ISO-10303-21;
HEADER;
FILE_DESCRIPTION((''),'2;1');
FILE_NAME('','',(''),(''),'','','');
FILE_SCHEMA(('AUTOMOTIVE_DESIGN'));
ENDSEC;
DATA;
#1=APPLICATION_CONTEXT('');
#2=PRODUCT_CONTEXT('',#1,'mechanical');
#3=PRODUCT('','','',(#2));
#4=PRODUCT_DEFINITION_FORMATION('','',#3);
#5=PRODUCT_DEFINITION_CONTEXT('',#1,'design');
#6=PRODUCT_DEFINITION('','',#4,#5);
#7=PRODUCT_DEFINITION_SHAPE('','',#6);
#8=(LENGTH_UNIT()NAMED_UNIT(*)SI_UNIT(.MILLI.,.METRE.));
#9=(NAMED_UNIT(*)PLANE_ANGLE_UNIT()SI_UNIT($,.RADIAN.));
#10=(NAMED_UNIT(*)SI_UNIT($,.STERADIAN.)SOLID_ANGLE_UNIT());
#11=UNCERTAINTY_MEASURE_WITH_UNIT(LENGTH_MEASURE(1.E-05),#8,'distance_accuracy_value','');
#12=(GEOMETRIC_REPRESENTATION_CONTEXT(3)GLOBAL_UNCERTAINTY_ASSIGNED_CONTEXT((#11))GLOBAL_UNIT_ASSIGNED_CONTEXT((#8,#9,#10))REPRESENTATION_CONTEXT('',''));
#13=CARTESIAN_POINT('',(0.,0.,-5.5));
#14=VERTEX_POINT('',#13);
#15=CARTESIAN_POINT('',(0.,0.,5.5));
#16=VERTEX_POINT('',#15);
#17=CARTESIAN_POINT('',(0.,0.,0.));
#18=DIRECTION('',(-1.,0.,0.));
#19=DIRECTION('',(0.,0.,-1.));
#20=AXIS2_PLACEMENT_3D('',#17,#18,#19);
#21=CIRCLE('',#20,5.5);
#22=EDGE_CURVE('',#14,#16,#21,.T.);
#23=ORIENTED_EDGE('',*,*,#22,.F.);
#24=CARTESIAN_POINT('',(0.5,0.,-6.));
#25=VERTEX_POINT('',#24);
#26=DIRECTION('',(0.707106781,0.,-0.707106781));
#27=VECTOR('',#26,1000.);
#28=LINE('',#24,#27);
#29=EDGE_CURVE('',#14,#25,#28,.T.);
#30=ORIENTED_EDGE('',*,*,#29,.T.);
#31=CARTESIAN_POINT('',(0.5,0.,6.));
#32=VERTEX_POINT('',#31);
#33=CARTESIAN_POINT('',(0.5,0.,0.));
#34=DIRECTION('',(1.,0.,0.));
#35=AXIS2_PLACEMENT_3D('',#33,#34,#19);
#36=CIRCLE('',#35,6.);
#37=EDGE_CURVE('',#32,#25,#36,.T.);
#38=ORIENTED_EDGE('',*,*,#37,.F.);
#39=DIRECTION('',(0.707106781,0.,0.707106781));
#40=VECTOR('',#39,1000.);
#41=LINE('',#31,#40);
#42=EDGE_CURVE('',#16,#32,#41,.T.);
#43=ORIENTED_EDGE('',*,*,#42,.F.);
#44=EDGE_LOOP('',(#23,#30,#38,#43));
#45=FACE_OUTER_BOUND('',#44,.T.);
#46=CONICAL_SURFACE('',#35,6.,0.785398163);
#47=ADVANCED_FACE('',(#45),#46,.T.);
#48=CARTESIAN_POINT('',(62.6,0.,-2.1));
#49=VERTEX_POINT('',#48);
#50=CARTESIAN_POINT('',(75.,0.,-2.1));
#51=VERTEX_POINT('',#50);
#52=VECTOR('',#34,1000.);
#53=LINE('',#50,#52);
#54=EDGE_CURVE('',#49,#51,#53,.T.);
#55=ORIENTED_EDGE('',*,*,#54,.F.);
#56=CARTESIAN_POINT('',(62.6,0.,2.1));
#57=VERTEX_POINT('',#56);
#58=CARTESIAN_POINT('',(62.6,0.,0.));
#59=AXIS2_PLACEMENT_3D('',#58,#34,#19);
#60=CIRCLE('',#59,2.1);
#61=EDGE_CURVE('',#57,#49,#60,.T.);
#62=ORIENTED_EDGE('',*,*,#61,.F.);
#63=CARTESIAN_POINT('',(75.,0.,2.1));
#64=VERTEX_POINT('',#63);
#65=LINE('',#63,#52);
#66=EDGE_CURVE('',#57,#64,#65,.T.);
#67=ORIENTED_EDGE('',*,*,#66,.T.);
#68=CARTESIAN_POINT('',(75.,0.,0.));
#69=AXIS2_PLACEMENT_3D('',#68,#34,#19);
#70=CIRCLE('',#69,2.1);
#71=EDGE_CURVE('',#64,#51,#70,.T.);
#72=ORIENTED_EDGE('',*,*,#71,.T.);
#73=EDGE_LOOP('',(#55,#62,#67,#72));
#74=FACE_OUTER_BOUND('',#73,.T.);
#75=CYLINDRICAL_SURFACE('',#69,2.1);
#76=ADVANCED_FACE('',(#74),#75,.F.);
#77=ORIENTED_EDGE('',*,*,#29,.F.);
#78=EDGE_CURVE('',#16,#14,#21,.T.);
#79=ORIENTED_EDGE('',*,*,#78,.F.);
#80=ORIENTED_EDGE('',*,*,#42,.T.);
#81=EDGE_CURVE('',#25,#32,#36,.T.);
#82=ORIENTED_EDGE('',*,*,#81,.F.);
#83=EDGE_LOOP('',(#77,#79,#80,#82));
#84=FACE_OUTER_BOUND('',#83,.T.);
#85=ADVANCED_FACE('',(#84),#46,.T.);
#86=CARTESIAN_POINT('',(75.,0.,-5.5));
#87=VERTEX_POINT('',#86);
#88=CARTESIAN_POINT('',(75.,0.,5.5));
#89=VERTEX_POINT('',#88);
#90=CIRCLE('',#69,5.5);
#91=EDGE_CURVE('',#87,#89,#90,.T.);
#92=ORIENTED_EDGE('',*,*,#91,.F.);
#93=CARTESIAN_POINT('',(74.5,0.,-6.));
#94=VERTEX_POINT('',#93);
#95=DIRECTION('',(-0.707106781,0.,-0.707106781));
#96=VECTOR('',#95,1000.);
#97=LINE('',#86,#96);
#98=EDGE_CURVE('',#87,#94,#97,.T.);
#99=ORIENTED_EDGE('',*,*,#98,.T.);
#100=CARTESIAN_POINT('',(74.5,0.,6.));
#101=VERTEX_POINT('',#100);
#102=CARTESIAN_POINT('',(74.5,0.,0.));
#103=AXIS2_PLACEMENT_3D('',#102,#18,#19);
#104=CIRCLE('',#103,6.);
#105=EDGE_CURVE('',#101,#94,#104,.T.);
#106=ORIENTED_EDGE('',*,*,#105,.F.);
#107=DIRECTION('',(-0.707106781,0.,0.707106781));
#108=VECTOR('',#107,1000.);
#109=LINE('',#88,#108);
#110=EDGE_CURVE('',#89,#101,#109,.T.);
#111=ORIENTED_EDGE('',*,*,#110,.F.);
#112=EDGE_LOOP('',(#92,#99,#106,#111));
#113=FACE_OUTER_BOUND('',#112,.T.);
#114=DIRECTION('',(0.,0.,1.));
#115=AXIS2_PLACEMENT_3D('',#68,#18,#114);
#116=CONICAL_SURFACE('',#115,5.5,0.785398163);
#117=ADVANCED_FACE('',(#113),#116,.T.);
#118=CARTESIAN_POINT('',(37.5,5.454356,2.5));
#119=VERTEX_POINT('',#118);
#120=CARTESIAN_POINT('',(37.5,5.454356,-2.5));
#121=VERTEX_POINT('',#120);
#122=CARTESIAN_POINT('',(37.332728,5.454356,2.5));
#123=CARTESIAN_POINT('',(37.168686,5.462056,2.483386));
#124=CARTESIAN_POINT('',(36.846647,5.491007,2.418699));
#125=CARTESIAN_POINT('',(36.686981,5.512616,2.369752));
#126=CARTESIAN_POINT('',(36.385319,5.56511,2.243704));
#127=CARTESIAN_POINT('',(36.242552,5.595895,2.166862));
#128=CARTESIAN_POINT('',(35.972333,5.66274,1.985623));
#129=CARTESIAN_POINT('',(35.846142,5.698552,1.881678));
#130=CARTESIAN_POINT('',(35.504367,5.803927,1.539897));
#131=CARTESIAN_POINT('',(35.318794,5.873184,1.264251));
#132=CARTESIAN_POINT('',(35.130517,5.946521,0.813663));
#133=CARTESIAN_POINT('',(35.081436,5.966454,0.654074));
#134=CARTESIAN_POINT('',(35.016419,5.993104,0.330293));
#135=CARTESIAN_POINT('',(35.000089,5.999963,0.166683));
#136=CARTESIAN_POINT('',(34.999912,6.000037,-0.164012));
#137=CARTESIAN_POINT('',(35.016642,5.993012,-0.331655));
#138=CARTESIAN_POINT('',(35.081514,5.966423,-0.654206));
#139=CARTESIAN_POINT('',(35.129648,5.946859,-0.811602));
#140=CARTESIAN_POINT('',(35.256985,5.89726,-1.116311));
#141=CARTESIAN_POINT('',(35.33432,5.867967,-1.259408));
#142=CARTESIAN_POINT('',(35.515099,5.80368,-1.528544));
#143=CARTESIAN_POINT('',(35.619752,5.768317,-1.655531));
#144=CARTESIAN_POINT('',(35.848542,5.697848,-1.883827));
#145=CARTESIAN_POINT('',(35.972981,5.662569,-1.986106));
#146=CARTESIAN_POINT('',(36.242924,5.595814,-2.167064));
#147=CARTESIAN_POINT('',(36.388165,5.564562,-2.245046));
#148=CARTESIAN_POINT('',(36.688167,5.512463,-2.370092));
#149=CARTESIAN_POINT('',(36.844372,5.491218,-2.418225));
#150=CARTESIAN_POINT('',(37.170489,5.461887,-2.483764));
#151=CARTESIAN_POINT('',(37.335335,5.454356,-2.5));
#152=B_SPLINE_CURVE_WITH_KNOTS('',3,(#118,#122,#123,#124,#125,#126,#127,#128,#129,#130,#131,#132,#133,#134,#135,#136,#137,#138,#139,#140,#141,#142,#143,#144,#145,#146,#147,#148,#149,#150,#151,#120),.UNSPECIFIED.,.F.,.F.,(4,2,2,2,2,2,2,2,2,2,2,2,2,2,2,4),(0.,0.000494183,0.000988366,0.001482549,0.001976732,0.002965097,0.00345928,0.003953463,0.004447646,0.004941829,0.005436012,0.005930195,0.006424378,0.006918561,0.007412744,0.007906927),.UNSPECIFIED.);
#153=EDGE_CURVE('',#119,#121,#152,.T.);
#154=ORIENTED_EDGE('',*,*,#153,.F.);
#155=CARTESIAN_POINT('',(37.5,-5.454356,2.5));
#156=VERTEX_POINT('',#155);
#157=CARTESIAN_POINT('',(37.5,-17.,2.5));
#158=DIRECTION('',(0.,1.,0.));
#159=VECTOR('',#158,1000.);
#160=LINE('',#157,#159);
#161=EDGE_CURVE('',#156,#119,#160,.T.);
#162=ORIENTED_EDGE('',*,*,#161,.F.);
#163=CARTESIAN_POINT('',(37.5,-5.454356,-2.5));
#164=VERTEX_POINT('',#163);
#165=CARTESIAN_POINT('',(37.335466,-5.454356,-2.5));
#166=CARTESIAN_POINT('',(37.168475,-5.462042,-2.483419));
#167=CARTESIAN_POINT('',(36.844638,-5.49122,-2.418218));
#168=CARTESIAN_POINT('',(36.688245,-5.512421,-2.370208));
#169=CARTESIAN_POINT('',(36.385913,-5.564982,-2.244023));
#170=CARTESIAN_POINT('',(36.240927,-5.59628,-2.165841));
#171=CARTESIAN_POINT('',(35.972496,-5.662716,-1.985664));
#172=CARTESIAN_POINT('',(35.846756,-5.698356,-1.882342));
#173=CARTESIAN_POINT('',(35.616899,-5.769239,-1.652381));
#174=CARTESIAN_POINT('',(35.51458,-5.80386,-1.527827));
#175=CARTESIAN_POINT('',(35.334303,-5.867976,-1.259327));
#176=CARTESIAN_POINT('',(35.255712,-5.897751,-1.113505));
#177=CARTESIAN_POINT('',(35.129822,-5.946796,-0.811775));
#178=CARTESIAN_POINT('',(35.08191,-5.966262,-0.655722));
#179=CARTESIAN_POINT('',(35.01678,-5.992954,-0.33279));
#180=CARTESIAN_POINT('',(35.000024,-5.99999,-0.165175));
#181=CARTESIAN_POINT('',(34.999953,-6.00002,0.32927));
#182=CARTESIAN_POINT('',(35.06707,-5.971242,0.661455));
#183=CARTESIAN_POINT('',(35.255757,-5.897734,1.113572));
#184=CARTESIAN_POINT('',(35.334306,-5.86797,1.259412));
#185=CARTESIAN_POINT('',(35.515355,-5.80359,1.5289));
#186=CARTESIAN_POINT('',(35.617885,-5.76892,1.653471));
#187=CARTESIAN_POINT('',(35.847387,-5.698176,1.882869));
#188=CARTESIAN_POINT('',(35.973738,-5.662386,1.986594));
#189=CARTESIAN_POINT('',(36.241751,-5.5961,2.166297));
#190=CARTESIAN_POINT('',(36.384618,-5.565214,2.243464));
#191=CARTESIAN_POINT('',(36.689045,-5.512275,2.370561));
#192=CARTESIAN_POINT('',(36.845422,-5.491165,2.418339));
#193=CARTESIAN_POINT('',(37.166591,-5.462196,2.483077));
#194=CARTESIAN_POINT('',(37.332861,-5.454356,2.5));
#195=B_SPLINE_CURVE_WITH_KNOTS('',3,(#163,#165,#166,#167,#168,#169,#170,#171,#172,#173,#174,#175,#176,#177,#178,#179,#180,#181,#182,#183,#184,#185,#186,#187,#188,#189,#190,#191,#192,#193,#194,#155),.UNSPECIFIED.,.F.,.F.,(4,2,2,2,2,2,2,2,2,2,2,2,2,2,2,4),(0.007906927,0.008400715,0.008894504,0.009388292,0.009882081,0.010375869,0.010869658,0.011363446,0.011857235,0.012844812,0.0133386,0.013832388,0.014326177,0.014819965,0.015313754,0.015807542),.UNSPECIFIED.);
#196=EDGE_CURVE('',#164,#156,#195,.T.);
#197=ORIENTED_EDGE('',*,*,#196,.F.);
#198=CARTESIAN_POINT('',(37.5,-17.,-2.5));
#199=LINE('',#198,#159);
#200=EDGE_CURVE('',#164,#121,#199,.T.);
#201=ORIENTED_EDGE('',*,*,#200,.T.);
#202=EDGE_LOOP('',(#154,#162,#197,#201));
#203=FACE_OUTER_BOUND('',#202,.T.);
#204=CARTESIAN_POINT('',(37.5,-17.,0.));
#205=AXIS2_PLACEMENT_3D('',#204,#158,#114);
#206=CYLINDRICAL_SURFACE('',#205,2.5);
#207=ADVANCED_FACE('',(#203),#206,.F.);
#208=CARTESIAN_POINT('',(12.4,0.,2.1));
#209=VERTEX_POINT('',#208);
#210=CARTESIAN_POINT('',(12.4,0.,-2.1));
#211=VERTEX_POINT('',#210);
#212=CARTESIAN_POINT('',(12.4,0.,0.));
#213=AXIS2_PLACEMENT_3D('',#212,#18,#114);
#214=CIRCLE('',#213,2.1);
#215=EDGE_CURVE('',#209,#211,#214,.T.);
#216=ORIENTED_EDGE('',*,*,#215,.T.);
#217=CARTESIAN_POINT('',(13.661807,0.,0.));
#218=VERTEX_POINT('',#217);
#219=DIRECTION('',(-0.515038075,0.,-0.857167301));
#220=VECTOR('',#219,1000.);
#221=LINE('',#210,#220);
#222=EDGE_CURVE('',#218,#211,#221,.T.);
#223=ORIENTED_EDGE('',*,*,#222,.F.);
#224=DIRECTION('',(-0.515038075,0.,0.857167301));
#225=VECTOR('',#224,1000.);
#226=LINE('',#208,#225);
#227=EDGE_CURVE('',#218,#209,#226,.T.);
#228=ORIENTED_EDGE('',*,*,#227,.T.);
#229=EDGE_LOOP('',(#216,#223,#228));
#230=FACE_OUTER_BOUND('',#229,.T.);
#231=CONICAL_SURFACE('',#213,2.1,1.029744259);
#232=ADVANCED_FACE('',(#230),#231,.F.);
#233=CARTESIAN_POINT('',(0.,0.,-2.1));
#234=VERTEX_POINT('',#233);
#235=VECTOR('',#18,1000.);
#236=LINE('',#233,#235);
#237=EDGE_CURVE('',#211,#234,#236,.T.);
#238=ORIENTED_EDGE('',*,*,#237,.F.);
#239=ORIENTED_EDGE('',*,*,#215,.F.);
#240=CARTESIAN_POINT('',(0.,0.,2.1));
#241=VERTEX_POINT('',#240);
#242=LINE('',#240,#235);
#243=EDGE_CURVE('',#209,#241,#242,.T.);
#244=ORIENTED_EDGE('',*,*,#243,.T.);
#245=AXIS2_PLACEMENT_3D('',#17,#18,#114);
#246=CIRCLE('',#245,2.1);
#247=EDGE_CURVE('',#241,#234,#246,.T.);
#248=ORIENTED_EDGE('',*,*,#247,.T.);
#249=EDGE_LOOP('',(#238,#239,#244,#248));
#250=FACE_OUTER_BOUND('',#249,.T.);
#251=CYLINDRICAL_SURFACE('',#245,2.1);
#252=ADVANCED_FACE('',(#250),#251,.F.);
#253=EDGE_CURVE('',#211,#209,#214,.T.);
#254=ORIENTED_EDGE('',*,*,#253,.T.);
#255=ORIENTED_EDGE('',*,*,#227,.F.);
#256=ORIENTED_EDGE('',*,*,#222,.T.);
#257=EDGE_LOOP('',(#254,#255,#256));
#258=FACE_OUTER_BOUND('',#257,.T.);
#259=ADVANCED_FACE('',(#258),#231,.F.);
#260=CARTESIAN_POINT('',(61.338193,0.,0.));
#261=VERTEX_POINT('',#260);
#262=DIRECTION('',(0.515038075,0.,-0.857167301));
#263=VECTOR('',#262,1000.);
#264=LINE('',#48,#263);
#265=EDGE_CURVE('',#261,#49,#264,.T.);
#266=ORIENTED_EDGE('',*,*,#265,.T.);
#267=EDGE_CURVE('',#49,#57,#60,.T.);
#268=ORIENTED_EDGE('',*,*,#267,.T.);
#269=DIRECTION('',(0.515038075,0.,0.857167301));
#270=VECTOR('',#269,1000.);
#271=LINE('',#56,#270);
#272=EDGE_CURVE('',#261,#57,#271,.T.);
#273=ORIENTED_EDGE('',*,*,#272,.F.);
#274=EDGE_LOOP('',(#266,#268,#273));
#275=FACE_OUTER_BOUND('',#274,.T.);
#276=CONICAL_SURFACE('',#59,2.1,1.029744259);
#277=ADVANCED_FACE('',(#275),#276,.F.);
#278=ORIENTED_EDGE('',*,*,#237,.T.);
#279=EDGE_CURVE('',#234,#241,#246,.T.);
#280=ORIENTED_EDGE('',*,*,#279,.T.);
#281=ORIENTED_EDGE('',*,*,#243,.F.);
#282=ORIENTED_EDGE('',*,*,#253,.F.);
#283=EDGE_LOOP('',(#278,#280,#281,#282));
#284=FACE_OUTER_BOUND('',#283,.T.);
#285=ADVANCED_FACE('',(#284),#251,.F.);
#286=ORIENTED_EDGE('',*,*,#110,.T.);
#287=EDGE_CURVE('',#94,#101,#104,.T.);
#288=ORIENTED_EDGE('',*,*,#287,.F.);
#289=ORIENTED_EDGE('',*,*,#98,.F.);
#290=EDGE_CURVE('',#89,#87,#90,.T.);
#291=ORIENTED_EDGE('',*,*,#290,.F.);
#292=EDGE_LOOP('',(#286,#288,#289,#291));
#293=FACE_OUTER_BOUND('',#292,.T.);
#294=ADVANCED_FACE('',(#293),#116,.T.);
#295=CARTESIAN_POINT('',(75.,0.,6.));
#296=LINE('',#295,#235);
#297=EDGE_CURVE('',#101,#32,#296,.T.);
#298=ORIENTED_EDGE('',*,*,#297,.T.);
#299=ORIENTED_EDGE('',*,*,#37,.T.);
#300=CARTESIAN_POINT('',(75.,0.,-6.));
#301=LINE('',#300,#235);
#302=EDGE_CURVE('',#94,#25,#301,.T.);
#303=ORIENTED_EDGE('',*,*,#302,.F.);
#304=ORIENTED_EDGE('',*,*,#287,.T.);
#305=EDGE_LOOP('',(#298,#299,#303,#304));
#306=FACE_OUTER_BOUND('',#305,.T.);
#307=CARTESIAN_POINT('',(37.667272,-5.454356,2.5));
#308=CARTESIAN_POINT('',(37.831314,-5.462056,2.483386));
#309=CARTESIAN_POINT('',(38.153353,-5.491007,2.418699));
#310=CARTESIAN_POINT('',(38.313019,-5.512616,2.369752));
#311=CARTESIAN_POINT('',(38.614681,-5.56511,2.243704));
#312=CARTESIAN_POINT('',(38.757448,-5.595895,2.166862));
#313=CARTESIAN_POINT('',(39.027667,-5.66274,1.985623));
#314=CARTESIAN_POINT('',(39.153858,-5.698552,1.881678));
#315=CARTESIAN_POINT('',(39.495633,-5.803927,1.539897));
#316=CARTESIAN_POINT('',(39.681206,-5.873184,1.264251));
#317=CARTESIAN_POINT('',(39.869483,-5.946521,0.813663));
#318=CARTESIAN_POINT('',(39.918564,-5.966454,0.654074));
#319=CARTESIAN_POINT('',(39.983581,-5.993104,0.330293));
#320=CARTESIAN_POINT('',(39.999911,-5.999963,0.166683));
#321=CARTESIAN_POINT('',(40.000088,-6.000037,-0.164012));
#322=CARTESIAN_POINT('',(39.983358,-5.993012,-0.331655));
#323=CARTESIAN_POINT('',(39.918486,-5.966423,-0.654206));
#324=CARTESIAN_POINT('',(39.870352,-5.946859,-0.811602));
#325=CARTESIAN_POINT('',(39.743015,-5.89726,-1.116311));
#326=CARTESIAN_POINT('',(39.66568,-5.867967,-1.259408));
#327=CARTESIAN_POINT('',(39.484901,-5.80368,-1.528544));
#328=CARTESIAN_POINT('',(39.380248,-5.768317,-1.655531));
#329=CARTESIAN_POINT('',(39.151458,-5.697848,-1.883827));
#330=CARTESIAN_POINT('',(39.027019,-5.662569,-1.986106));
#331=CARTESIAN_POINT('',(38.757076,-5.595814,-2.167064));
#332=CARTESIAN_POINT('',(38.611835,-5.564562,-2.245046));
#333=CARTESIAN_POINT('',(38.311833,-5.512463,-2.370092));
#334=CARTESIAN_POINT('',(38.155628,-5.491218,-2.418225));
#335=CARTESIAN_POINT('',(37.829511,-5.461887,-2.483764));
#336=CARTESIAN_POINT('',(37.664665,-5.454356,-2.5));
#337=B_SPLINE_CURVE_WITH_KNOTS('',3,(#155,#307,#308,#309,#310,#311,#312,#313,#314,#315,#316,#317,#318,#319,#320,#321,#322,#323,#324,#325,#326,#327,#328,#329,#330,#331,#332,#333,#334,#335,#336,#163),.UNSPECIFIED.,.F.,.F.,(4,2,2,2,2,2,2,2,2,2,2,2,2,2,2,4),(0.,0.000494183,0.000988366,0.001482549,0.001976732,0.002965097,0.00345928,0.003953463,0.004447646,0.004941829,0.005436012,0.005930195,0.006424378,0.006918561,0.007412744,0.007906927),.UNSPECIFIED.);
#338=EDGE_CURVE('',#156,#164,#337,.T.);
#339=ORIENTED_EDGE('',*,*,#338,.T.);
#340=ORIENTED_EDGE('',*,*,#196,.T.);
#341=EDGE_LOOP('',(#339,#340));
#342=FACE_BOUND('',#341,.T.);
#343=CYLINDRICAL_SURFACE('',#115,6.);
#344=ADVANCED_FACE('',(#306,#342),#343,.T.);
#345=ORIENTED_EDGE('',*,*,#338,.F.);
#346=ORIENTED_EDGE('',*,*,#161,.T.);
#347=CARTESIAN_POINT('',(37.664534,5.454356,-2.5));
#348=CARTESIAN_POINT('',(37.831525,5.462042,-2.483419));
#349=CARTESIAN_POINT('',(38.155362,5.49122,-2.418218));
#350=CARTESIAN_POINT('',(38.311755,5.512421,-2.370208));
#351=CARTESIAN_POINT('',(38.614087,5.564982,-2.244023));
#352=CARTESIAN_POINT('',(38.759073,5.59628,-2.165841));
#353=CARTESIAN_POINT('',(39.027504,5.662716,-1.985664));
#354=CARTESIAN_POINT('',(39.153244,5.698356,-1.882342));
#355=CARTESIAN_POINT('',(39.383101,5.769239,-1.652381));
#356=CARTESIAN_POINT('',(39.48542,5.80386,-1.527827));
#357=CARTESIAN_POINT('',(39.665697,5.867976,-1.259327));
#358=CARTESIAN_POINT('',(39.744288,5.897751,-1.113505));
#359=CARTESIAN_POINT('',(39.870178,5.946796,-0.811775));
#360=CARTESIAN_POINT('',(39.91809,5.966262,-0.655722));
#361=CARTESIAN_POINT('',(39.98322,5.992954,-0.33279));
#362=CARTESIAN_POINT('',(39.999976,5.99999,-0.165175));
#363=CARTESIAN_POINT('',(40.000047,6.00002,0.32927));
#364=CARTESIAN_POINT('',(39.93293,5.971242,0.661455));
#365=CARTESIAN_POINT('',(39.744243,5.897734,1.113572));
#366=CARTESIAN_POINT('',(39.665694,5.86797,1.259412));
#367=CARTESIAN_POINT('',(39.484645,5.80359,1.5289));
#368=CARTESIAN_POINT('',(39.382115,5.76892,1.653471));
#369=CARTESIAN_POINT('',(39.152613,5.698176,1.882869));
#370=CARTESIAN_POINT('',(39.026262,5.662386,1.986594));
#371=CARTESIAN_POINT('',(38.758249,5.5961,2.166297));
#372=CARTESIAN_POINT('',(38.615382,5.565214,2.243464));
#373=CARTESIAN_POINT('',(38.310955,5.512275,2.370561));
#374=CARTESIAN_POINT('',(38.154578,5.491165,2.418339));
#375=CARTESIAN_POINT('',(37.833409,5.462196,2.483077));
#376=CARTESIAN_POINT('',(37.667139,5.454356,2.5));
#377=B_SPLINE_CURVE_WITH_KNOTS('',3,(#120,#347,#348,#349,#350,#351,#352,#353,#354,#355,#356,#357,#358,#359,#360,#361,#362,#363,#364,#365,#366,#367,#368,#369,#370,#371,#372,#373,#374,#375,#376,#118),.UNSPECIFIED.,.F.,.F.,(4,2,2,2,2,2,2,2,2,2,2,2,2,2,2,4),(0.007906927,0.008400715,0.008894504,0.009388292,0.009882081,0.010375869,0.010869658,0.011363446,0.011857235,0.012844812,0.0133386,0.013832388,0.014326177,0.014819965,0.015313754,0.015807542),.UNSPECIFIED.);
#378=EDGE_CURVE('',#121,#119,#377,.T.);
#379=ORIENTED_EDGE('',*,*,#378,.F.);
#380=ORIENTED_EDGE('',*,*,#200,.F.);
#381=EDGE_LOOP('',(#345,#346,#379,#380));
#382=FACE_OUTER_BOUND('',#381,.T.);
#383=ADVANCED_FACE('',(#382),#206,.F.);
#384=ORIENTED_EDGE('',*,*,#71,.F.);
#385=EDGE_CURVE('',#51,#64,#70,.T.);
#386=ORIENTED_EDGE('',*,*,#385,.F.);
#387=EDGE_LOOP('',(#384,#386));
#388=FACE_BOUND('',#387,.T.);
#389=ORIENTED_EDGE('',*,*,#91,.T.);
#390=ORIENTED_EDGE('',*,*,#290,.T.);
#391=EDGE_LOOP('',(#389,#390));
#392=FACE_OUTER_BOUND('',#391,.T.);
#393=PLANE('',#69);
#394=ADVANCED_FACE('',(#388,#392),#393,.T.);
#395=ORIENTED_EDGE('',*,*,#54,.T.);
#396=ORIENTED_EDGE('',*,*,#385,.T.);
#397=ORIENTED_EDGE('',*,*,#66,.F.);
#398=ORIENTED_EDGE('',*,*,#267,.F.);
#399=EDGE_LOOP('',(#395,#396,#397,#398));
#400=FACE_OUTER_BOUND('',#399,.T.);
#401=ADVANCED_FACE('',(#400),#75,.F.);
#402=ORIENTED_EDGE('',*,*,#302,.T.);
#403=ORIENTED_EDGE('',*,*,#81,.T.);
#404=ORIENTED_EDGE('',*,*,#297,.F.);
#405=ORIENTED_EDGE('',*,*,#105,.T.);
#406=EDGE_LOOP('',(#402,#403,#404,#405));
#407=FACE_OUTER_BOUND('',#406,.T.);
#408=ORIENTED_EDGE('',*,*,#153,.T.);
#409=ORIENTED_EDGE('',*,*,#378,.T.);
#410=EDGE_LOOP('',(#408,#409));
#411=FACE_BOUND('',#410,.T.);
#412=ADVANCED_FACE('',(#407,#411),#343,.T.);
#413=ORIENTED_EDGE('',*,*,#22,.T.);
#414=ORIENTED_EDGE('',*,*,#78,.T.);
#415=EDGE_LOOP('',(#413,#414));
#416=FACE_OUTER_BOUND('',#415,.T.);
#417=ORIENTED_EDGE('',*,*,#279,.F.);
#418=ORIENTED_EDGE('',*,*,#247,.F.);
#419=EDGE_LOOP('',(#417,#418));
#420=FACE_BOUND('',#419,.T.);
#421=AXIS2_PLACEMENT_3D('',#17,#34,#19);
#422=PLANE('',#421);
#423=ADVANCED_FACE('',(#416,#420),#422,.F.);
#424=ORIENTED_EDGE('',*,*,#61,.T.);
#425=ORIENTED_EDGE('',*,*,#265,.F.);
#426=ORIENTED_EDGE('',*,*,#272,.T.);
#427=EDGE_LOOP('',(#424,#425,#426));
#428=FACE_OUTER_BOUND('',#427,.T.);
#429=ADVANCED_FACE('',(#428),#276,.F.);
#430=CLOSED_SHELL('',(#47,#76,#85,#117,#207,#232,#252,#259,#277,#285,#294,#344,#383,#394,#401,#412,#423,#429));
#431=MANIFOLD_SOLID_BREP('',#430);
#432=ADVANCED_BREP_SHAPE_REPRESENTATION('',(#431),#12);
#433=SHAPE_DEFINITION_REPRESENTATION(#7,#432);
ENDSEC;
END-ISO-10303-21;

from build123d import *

# Parameters (mm, degrees)
SKETCH1_R             = 6
BOSS_EXTRUDE1_DEPTH   = 75
M5_TAPPED_HOLE1_D     = 4.2
M5_TAPPED_HOLE1_DEPTH = 12.4
M5_TAPPED_HOLE1_TIP   = 1.2618073
M5_TAPPED_HOLE2_D     = 4.2
M5_TAPPED_HOLE2_DEPTH = 12.4
M5_TAPPED_HOLE2_TIP   = 1.2618073
CHAMFER1_SIZE         = 0.5
SKETCH6_R             = 2.5
CUT_EXTRUDE1_DEPTH    = 17


with BuildPart() as part:
    # Sketch1 → Boss-Extrude1 (new body)
    with BuildSketch(Plane(origin=(0, 0, 0), x_dir=(0, 0, -1), z_dir=(1, 0, 0))):
        Circle(SKETCH1_R)
    extrude(amount=BOSS_EXTRUDE1_DEPTH)

    # M5 Tapped Hole1
    with Locations(Plane(origin=(75, 0, 0), x_dir=(0, 0, -1), z_dir=(1, 0, 0))):
        with Locations((0, 0)):
            Hole(M5_TAPPED_HOLE1_D / 2, depth=M5_TAPPED_HOLE1_DEPTH)
            with Locations((0, 0, -(M5_TAPPED_HOLE1_DEPTH + M5_TAPPED_HOLE1_TIP / 2))):  # 118° drill point
                Cone(0, M5_TAPPED_HOLE1_D / 2, M5_TAPPED_HOLE1_TIP, mode=Mode.SUBTRACT)

    # M5 Tapped Hole2
    with Locations(Plane.ZY):
        with Locations((0, 0)):
            Hole(M5_TAPPED_HOLE2_D / 2, depth=M5_TAPPED_HOLE2_DEPTH)
            with Locations((0, 0, -(M5_TAPPED_HOLE2_DEPTH + M5_TAPPED_HOLE2_TIP / 2))):  # 118° drill point
                Cone(0, M5_TAPPED_HOLE2_D / 2, M5_TAPPED_HOLE2_TIP, mode=Mode.SUBTRACT)

    # Chamfer1
    chamfer1_edges = [part.edges().sort_by_distance(p)[0] for p in [
        (0, 0, 6),
        (75, 0, 6),
    ]]
    chamfer(chamfer1_edges, length=CHAMFER1_SIZE)

    # Sketch6 → Cut-Extrude1 (cut, symmetric)
    with BuildSketch(Plane(origin=(0, 0, 0), x_dir=(1, 0, 0), z_dir=(0, 1, 0))):
        with Locations(Location((37.5, 0, 0), (0, 0, 270))):
            Circle(SKETCH6_R)
    extrude(amount=CUT_EXTRUDE1_DEPTH, both=True, mode=Mode.SUBTRACT)


solid = part.part
